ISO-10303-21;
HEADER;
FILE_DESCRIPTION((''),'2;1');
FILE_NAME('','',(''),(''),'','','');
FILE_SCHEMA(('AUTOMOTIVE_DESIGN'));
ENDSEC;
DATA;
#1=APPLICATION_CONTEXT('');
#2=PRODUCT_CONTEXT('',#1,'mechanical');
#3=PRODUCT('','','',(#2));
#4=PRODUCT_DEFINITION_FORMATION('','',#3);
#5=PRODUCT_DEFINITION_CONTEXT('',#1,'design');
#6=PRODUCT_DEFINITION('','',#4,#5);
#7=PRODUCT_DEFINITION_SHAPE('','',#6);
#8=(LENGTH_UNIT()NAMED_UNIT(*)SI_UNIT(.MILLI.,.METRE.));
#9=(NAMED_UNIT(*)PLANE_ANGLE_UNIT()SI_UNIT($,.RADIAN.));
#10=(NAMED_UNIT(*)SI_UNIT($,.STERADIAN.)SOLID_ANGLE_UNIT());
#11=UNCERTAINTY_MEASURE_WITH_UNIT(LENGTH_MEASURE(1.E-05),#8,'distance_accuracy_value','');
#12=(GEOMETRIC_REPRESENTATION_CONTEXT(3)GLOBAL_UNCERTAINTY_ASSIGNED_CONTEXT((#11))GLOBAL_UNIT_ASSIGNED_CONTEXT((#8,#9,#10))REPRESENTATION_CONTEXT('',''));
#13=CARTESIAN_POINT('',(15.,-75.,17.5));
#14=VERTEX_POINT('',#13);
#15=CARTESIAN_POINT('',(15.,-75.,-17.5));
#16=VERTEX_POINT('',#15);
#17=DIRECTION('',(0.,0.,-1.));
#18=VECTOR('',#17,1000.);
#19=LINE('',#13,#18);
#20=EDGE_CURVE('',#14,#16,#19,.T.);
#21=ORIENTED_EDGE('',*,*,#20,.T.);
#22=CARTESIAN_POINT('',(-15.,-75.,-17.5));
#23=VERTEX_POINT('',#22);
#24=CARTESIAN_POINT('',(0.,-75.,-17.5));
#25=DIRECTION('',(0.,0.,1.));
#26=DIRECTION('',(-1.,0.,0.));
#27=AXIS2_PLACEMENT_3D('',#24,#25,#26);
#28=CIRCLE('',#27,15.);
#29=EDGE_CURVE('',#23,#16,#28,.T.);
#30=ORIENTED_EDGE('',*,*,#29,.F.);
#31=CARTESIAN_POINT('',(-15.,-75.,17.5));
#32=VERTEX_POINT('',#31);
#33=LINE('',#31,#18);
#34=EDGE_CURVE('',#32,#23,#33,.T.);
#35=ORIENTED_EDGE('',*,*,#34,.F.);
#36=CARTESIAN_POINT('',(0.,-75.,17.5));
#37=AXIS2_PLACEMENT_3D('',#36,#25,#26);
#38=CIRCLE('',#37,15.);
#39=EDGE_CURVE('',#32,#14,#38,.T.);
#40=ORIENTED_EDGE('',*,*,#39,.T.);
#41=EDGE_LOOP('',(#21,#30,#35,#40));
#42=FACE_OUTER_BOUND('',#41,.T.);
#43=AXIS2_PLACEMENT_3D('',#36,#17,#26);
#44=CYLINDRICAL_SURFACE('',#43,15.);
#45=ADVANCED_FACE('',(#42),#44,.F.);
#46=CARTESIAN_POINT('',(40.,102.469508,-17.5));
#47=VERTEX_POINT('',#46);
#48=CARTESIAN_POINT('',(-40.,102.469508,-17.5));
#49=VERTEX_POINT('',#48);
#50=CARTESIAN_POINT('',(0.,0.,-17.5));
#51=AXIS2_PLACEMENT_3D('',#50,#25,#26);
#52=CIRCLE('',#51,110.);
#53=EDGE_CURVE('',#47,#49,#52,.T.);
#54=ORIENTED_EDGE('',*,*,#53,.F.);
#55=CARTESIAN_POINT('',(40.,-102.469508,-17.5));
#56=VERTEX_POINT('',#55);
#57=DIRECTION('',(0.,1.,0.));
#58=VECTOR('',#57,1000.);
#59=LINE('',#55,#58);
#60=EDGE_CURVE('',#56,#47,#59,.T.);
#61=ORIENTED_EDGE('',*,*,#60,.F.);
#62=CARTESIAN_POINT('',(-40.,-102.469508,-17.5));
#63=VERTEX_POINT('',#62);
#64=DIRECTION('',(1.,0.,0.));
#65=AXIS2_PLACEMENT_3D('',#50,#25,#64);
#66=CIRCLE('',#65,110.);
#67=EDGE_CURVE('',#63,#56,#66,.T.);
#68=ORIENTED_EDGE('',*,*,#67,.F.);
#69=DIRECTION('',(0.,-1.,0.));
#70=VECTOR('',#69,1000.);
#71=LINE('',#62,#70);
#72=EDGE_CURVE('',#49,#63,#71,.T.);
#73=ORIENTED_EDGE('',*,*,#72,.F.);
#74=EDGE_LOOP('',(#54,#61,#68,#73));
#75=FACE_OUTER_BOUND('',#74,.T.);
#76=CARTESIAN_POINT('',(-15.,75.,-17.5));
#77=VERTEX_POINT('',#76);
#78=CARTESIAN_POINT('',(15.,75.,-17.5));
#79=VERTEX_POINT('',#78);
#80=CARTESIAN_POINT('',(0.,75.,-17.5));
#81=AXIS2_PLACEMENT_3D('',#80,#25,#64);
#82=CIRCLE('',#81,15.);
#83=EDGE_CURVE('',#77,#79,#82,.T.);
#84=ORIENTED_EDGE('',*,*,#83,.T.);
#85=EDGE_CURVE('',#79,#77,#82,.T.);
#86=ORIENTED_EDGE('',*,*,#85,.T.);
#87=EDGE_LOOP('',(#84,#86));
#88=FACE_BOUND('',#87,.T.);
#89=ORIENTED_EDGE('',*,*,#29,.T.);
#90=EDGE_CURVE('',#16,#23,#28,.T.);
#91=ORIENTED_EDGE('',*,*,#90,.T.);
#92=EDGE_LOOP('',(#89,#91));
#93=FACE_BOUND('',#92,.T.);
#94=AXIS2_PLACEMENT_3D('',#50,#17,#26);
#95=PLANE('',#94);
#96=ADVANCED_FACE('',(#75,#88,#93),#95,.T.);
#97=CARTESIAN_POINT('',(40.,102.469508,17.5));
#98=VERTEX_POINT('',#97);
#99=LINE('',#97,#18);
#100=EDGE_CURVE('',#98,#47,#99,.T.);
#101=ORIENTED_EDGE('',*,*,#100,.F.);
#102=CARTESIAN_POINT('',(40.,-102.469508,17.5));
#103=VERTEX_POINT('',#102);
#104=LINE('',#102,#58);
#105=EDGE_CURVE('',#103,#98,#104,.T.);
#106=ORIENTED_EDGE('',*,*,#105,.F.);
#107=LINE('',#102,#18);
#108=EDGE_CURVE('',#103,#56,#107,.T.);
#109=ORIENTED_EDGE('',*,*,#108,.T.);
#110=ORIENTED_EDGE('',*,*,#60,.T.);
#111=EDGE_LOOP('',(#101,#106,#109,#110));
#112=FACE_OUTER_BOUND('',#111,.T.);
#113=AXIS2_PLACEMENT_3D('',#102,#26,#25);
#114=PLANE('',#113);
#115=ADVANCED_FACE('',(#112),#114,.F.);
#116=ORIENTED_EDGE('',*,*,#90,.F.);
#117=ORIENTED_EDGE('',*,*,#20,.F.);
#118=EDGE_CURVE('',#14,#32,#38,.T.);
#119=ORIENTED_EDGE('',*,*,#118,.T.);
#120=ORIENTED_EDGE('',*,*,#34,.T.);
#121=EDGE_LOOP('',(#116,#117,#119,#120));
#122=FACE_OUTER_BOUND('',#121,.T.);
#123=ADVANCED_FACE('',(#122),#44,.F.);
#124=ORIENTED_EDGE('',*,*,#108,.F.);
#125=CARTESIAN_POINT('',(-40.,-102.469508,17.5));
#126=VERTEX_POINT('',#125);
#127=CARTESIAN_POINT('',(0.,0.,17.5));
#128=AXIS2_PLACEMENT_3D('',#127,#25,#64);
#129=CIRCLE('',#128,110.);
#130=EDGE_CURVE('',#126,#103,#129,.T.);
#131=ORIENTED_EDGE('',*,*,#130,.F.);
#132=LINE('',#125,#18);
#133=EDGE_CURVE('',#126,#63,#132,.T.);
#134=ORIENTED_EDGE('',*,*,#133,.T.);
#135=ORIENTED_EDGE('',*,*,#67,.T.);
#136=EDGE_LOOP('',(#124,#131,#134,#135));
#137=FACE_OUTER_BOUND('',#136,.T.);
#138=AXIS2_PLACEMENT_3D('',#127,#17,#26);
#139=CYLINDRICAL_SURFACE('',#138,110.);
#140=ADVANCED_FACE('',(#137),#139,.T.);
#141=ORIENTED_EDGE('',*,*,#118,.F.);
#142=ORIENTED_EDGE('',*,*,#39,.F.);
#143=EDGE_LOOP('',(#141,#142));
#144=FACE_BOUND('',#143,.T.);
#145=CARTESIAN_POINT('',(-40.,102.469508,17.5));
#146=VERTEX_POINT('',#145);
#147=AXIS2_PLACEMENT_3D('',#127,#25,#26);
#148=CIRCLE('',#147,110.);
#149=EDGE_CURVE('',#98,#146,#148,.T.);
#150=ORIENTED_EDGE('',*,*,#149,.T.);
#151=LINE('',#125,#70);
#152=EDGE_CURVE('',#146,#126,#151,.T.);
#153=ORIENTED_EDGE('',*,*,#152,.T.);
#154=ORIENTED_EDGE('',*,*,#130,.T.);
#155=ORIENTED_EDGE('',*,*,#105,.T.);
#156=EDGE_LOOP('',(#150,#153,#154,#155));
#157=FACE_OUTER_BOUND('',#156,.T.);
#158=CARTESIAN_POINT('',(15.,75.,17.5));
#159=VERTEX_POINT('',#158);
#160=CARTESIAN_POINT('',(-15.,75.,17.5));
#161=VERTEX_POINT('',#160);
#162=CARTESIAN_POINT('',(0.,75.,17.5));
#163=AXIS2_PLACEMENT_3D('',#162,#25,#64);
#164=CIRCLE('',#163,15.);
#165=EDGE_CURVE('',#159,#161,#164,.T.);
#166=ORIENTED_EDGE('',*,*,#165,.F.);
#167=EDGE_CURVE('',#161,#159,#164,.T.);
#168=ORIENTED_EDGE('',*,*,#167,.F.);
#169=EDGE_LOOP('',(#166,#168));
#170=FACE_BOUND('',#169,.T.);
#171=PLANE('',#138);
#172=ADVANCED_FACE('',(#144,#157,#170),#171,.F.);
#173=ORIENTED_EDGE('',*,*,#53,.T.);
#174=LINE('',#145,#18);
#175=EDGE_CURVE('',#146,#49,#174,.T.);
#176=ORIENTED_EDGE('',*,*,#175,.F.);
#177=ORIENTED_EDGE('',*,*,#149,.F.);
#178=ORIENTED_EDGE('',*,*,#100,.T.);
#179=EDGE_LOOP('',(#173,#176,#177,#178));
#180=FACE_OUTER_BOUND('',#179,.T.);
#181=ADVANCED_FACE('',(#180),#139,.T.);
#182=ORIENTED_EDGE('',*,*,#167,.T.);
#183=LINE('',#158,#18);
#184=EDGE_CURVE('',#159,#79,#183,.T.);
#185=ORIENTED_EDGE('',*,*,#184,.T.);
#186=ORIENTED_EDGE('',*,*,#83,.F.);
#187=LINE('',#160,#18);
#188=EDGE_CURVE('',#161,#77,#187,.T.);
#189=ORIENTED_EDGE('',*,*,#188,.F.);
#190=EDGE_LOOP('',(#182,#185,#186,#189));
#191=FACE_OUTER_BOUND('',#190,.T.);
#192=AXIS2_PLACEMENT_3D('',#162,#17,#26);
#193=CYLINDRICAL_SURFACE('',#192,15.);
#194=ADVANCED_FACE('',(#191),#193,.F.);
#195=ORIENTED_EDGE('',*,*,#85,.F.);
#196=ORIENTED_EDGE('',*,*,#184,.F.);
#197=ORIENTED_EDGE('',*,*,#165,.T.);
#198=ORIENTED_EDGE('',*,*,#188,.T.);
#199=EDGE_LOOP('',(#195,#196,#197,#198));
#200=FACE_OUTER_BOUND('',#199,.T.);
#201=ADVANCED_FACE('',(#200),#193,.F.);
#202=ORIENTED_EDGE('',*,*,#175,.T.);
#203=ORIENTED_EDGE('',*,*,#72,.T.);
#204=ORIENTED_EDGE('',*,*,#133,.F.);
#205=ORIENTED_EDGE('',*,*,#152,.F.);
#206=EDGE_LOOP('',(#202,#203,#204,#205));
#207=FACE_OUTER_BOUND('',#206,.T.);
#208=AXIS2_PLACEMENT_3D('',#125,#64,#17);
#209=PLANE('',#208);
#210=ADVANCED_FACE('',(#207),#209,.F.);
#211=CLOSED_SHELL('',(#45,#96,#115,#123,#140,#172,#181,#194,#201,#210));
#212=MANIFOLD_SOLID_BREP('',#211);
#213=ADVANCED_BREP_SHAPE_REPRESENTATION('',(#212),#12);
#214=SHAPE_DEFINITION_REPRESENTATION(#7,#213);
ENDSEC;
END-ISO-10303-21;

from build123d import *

# Parameters (mm, degrees)
PLATE_PROFILE_WITH_BORES_R = 15
CROSSHEAD_PLATE_35MM_DEPTH = 17.5


with BuildPart() as part:
    # Plate Profile with Bores → Crosshead Plate 35mm (new, symmetric)
    with BuildSketch(Plane.XY):
        with BuildLine():
            Line((-40, -102.46950766), (-40, 102.46950766))
            ThreePointArc((-40, 102.46950766), (0, 110), (40, 102.46950766))
            Line((40, 102.46950766), (40, -102.46950766))
            ThreePointArc((40, -102.46950766), (0, -110), (-40, -102.46950766))
        make_face()
        with Locations((0, 75)):
            Circle(PLATE_PROFILE_WITH_BORES_R, mode=Mode.SUBTRACT)
        with Locations(Location((0, -75, 0), (0, 0, 180))):
            Circle(PLATE_PROFILE_WITH_BORES_R, mode=Mode.SUBTRACT)
    extrude(amount=CROSSHEAD_PLATE_35MM_DEPTH, both=True)


solid = part.part
